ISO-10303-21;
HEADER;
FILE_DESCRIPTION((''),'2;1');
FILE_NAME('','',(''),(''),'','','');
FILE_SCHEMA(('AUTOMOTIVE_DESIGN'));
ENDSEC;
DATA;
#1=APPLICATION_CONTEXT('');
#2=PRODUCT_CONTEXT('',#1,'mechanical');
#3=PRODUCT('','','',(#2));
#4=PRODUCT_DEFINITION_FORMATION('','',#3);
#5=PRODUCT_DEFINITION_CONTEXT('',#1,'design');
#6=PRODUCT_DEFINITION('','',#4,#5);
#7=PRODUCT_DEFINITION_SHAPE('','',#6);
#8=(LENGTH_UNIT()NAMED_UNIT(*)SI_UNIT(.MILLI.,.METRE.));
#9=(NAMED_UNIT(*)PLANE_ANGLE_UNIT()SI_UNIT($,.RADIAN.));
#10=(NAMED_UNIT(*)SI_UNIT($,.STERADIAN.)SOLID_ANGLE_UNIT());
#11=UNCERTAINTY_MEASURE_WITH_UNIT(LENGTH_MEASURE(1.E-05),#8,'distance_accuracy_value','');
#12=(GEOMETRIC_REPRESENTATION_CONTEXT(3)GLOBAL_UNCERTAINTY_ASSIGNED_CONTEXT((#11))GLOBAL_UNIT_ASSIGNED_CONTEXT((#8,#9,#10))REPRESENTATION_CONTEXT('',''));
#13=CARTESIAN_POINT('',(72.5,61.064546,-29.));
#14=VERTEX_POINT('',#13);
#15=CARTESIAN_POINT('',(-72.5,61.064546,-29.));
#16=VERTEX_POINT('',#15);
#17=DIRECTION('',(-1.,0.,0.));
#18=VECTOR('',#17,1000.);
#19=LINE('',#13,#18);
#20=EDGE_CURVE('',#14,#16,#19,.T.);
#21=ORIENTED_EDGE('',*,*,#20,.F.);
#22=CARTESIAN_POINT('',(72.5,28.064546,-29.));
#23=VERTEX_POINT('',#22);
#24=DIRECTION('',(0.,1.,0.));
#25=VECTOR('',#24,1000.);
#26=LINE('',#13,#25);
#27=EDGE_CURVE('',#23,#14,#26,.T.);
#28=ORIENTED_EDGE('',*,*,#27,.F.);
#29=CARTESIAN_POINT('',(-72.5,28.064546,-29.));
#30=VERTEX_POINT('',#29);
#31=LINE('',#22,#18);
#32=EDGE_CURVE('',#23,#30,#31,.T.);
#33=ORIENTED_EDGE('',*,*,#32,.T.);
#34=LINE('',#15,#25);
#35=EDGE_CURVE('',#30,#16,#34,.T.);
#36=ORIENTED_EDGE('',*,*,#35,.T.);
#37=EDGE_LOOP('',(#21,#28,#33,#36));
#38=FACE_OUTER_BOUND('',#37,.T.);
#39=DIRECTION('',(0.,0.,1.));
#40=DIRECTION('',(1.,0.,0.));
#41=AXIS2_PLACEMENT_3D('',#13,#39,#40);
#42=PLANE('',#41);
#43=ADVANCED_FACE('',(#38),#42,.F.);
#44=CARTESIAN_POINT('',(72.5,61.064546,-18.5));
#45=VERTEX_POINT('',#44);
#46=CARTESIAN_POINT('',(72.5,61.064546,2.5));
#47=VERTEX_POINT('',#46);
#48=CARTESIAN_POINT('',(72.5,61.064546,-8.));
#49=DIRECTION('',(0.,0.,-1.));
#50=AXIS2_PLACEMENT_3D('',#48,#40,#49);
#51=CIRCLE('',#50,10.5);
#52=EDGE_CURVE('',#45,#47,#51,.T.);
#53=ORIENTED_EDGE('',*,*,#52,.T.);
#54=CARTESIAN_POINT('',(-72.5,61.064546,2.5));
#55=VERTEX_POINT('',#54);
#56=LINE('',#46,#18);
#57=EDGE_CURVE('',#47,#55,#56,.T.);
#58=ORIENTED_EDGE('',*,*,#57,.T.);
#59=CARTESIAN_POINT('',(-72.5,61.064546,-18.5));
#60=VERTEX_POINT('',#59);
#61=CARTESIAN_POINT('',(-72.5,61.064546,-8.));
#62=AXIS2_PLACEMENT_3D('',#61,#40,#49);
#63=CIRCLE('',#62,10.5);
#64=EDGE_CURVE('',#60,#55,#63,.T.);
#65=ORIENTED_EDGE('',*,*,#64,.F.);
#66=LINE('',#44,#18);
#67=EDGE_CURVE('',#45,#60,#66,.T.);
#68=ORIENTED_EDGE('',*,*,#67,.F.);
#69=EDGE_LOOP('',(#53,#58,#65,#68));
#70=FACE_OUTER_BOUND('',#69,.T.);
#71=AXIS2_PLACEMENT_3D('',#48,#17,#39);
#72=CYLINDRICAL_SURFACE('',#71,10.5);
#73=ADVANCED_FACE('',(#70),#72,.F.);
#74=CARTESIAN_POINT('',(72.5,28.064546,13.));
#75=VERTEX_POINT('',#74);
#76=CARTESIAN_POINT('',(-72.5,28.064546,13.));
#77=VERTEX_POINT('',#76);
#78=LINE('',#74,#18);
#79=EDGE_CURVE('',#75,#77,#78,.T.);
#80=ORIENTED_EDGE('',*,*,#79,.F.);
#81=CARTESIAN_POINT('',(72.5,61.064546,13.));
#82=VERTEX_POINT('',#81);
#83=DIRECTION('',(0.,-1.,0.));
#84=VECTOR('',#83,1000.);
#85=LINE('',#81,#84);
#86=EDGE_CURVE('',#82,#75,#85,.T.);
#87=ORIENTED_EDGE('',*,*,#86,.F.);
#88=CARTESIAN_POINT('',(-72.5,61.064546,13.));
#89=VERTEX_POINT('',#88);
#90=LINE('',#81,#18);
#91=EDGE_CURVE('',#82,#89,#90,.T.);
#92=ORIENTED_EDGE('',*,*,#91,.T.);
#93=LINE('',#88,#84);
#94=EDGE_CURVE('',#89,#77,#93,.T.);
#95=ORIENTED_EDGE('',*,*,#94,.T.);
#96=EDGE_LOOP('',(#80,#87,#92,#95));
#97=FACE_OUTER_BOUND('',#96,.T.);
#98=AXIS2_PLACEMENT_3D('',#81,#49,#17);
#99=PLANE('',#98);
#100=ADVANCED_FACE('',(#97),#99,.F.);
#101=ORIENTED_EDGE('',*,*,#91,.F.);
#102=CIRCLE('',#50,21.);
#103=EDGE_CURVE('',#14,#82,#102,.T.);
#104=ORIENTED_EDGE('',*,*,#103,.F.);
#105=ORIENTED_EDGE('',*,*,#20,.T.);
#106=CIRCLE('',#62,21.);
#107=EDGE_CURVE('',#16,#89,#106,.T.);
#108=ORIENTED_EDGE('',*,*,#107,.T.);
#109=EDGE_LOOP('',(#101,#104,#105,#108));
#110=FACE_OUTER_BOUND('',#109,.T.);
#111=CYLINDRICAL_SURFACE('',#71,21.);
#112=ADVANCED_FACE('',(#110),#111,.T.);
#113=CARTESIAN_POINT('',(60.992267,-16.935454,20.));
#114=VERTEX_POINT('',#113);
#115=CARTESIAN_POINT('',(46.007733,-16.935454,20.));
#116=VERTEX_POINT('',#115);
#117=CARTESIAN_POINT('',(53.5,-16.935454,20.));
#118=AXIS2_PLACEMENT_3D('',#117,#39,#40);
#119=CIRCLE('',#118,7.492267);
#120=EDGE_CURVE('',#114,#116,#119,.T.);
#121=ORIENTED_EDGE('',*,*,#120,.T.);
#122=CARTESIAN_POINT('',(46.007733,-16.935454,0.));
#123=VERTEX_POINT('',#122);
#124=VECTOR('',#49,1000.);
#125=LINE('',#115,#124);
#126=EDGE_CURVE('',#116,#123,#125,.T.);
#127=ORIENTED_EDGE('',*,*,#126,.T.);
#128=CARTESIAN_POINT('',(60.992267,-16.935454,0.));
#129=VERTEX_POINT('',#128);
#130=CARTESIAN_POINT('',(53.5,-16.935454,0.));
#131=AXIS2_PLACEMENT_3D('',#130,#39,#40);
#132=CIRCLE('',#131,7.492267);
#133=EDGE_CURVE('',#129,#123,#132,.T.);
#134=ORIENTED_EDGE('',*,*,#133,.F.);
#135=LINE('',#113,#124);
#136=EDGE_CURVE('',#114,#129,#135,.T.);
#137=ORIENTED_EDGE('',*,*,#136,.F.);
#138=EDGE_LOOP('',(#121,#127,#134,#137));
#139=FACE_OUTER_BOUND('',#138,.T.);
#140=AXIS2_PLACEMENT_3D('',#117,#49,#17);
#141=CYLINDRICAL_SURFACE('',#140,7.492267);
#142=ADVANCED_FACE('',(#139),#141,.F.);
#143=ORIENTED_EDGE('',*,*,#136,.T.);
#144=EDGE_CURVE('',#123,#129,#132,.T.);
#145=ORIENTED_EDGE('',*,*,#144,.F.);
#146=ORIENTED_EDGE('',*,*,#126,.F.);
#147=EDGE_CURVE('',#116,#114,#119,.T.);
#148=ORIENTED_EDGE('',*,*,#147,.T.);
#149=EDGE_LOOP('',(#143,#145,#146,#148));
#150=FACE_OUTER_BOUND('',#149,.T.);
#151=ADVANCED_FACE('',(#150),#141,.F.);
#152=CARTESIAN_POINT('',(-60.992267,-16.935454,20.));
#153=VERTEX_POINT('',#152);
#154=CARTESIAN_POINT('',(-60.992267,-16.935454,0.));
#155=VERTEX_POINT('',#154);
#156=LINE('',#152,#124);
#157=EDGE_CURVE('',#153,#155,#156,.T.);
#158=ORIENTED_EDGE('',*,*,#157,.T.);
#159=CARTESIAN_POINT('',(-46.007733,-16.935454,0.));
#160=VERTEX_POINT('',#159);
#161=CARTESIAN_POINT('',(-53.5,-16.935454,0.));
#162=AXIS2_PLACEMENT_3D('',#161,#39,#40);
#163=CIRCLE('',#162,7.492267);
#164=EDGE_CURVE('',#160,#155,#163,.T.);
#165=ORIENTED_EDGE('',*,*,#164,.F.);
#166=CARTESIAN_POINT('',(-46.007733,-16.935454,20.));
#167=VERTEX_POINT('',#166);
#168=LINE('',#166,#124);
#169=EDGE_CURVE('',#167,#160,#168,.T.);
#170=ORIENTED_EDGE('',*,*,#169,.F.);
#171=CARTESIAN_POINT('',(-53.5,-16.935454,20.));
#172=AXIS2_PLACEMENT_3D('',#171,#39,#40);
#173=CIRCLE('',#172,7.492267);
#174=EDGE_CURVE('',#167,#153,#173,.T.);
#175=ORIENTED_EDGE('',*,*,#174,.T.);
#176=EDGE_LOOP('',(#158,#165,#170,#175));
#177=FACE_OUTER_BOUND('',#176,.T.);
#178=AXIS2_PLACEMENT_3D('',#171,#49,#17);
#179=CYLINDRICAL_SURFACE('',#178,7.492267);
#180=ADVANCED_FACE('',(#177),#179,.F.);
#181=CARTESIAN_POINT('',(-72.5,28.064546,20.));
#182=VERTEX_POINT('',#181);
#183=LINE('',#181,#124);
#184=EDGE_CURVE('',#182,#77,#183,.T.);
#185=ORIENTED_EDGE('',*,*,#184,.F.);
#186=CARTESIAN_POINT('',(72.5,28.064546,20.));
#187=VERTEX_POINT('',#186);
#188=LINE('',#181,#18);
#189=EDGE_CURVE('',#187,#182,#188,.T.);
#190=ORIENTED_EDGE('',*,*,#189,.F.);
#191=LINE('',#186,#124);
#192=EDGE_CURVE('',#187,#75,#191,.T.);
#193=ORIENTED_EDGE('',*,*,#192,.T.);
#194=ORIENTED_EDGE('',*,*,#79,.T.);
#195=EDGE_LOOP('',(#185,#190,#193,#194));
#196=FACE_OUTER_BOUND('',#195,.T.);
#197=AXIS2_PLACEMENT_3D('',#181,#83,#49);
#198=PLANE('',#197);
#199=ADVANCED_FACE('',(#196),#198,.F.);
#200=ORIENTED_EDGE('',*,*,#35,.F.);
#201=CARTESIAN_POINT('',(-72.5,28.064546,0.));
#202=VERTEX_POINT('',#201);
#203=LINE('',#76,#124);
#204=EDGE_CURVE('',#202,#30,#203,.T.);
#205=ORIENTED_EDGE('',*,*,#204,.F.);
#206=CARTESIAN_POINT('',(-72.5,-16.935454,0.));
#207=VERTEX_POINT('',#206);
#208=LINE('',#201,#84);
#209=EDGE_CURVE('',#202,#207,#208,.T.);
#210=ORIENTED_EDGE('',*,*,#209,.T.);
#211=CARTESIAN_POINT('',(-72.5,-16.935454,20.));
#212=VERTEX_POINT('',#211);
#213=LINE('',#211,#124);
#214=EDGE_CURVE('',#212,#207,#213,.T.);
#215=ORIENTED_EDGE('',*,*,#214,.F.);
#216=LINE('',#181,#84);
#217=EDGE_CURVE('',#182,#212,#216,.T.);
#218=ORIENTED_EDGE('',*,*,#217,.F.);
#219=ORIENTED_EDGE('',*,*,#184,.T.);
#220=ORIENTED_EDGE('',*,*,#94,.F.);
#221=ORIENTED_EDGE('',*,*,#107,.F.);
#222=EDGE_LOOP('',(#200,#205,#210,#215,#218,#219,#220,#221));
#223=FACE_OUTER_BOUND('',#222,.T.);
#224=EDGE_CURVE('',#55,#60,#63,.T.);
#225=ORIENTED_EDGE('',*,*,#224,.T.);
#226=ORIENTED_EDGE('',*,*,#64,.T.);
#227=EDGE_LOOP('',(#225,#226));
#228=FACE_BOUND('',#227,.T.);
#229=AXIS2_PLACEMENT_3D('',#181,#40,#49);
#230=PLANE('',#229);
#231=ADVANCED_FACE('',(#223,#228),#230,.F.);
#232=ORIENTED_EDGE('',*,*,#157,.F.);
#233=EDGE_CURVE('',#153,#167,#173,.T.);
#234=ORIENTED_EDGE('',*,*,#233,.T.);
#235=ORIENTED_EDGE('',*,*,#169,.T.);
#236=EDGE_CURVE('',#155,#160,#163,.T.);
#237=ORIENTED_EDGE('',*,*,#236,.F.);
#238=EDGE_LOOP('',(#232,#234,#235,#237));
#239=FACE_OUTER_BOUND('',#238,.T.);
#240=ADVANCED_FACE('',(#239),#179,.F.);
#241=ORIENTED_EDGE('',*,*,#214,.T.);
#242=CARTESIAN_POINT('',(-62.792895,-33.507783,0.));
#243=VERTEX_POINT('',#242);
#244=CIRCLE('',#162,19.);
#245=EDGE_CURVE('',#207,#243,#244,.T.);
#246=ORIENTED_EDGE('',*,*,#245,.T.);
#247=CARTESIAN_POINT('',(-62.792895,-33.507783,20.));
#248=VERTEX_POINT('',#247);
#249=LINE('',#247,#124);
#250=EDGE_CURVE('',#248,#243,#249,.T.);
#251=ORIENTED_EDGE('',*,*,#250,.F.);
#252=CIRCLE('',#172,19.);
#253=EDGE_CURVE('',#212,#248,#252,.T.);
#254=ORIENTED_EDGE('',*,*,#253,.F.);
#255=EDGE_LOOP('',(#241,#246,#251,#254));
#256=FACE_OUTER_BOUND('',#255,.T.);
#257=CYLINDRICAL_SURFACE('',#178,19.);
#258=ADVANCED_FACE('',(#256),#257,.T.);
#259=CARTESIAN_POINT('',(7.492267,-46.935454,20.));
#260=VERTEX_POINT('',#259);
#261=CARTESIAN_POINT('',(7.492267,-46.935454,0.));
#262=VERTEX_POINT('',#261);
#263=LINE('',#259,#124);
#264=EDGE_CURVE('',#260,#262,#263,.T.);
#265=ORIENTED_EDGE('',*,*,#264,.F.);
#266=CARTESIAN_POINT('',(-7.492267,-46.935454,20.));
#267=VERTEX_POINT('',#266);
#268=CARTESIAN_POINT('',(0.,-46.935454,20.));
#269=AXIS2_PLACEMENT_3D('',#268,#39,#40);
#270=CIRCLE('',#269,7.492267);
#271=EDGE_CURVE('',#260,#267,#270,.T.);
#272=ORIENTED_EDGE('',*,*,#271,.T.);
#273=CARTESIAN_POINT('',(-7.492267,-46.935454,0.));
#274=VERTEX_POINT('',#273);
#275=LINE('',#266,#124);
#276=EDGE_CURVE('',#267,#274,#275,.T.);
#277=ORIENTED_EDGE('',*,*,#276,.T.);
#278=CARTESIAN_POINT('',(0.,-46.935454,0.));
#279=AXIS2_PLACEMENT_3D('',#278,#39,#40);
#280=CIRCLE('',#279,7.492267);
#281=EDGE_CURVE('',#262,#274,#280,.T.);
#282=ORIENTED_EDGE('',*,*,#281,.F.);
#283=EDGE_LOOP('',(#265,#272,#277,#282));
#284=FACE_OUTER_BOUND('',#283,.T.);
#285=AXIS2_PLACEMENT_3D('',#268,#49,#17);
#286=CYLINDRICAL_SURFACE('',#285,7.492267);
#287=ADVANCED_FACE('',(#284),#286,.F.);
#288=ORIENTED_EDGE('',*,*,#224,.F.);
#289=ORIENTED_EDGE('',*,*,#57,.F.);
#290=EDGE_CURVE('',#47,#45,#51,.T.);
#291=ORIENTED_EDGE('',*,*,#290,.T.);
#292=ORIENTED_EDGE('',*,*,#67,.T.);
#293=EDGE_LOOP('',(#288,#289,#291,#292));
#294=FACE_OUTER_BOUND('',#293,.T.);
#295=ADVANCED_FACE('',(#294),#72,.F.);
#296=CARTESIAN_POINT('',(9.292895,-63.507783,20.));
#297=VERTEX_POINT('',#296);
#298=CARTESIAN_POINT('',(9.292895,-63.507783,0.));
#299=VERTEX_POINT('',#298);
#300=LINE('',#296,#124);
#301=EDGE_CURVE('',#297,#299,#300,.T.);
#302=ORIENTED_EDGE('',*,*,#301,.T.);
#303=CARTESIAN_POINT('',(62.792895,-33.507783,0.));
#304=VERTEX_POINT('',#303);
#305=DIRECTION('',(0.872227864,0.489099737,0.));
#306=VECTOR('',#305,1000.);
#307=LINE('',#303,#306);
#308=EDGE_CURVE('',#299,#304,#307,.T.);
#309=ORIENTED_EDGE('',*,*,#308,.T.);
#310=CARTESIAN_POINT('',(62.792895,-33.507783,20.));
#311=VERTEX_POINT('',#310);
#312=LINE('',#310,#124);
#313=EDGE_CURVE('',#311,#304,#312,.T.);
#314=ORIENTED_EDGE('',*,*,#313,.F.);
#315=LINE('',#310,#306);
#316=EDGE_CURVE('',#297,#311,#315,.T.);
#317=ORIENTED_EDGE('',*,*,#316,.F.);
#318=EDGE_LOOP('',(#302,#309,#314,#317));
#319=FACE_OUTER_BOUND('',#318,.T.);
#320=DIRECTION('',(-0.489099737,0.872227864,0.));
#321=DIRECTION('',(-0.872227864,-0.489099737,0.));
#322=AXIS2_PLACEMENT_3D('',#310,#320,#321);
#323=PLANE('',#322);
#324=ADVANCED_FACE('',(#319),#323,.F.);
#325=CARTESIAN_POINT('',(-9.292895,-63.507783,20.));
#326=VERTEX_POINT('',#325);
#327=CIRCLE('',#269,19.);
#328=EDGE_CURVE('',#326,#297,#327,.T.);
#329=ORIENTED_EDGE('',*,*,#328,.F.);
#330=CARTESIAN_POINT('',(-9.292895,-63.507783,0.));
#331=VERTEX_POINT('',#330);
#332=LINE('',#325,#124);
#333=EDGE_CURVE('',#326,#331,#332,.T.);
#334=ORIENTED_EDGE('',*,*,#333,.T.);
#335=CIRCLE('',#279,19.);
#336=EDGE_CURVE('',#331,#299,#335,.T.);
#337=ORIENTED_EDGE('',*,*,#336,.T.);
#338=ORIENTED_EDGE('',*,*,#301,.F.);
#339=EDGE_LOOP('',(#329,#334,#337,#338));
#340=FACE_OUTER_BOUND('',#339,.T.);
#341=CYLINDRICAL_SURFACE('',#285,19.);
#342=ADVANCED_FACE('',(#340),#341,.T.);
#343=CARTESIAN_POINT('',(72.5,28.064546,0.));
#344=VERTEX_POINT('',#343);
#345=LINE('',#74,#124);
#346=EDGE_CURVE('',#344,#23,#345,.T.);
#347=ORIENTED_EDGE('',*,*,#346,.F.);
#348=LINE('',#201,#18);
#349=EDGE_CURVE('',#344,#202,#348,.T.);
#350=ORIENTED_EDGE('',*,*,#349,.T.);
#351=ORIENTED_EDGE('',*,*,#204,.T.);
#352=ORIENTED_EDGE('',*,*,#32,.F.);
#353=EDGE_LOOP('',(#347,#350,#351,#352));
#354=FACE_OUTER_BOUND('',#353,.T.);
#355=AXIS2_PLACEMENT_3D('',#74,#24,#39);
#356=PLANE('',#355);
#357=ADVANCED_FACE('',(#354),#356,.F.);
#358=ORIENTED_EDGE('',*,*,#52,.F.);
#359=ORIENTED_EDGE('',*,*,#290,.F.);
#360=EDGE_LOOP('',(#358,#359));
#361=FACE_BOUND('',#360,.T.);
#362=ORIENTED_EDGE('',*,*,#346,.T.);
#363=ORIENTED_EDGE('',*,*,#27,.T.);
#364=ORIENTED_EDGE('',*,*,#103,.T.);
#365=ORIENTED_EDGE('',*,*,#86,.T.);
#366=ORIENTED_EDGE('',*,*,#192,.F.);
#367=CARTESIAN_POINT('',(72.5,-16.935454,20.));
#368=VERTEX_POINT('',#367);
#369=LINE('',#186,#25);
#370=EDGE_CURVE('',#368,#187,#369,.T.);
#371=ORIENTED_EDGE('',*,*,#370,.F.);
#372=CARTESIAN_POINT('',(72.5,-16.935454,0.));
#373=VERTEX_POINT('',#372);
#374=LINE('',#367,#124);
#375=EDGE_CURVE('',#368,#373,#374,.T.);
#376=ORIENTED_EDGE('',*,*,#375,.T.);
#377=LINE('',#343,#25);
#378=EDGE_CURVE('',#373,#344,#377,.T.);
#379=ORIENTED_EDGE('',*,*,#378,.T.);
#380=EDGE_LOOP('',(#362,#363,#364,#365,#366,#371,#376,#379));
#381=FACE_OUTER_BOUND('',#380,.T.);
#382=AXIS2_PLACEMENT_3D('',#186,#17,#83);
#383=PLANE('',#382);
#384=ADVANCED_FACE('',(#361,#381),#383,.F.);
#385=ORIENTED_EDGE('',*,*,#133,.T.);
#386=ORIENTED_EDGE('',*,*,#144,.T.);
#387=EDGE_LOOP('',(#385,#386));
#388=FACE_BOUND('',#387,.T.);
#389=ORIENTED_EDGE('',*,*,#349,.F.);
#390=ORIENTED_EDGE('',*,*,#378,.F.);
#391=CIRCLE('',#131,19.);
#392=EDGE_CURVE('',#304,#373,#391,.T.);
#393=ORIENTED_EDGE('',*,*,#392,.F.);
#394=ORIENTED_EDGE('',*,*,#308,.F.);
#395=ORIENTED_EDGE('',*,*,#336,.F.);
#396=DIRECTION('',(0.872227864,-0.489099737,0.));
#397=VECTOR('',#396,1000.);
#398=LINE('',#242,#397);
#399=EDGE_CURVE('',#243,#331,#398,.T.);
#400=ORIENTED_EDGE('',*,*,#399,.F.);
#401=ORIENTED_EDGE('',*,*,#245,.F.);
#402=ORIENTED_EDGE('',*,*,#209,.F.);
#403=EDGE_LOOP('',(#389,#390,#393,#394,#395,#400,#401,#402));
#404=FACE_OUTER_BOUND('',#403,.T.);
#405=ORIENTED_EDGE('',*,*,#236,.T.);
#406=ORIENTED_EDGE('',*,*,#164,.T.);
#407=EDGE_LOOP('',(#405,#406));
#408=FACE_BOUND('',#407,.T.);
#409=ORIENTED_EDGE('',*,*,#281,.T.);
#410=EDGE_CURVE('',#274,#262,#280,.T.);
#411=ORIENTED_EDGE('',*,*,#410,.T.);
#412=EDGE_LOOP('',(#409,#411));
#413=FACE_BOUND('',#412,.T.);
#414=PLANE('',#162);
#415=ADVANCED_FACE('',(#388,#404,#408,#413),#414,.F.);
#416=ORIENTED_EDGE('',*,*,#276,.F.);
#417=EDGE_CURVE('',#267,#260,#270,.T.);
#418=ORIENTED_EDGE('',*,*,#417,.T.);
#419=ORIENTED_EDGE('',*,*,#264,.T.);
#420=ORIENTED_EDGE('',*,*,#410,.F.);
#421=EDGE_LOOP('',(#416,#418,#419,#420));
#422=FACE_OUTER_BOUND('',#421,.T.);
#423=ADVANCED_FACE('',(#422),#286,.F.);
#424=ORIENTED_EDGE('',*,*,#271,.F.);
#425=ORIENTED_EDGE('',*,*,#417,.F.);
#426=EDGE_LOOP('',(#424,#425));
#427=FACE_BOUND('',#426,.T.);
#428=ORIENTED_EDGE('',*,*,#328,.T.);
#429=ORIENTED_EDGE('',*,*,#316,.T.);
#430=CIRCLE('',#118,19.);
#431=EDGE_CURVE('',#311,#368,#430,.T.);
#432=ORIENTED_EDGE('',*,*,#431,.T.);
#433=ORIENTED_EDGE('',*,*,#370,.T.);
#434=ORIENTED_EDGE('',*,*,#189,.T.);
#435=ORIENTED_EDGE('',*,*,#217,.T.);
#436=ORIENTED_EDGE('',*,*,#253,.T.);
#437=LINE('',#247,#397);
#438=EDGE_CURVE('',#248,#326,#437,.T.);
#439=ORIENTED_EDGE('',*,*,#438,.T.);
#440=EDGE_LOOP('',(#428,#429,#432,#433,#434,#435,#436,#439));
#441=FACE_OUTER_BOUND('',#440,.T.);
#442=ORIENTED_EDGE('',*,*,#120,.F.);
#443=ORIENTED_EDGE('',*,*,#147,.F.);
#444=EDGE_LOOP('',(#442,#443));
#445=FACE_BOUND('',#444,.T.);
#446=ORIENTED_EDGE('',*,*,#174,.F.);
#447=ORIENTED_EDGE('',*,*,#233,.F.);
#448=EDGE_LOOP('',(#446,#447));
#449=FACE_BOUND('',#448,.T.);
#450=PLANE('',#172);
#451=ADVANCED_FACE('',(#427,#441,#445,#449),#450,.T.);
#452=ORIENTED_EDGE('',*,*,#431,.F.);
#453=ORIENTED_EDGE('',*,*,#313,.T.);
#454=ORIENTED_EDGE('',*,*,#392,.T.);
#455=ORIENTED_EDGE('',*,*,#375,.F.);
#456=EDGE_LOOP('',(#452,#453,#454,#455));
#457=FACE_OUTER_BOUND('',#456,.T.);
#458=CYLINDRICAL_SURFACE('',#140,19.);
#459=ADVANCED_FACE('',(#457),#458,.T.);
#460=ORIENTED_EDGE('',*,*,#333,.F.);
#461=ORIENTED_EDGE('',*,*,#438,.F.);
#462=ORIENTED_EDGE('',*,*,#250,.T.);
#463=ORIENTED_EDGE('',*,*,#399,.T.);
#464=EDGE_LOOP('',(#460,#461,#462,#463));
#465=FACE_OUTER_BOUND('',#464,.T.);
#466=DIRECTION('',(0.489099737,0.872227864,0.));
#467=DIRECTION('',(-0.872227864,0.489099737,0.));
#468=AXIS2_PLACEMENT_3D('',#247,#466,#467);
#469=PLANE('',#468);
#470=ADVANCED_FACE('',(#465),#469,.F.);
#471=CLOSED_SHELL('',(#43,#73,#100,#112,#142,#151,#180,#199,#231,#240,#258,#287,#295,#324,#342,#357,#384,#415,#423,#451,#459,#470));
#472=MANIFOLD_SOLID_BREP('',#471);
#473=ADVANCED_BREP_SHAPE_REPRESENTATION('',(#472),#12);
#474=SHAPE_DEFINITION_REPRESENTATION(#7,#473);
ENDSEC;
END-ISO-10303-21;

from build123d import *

# Parameters (mm, degrees)
BASE_PLATE_PROFILE_R      = 7.492267371
BASE_PLATE_20MM_DEPTH     = 20
HINGE_KNUCKLE_PROFILE_R   = 10.5
HINGE_KNUCKLE_145MM_DEPTH = 72.5


with BuildPart() as part:
    # Base Plate Profile → Base Plate 20mm (new body)
    with BuildSketch(Plane.XY):
        with BuildLine():
            Line((-72.5, 28.064546487), (72.5, 28.064546487))
            Line((72.5, 28.064546487), (72.5, -16.935453513))
            ThreePointArc((72.5, -16.935453513), (69.894587599, -26.538447706), (62.792895003, -33.507782934))
            Line((62.792895003, -33.507782934), (9.292895003, -63.507782934))
            ThreePointArc((9.292895003, -63.507782934), (0, -65.935453513), (-9.292895003, -63.507782934))
            Line((-9.292895003, -63.507782934), (-62.792895003, -33.507782934))
            ThreePointArc((-62.792895003, -33.507782934), (-69.894587599, -26.538447706), (-72.5, -16.935453513))
            Line((-72.5, -16.935453513), (-72.5, 28.064546487))
        make_face()
        with Locations((0, -46.935453513)):
            Circle(BASE_PLATE_PROFILE_R, mode=Mode.SUBTRACT)
        with Locations((53.5, -16.935453513)):
            Circle(BASE_PLATE_PROFILE_R, mode=Mode.SUBTRACT)
        with Locations((-53.5, -16.935453513)):
            Circle(BASE_PLATE_PROFILE_R, mode=Mode.SUBTRACT)
    extrude(amount=BASE_PLATE_20MM_DEPTH)

    # Hinge Knuckle Profile → Hinge Knuckle 145mm (add, symmetric)
    with BuildSketch(Plane(origin=(0, 0, 0), x_dir=(0, 0, -1), z_dir=(1, 0, 0))):
        with BuildLine():
            Line((29, 61.064546487), (29, 28.064546487))
            Line((29, 28.064546487), (-13, 28.064546487))
            Line((-13, 28.064546487), (-13, 61.064546487))
            ThreePointArc((-13, 61.064546487), (8, 82.064546487), (29, 61.064546487))
        make_face()
        with Locations((8, 61.064546487)):
            Circle(HINGE_KNUCKLE_PROFILE_R, mode=Mode.SUBTRACT)
    extrude(amount=HINGE_KNUCKLE_145MM_DEPTH, both=True)


solid = part.part
